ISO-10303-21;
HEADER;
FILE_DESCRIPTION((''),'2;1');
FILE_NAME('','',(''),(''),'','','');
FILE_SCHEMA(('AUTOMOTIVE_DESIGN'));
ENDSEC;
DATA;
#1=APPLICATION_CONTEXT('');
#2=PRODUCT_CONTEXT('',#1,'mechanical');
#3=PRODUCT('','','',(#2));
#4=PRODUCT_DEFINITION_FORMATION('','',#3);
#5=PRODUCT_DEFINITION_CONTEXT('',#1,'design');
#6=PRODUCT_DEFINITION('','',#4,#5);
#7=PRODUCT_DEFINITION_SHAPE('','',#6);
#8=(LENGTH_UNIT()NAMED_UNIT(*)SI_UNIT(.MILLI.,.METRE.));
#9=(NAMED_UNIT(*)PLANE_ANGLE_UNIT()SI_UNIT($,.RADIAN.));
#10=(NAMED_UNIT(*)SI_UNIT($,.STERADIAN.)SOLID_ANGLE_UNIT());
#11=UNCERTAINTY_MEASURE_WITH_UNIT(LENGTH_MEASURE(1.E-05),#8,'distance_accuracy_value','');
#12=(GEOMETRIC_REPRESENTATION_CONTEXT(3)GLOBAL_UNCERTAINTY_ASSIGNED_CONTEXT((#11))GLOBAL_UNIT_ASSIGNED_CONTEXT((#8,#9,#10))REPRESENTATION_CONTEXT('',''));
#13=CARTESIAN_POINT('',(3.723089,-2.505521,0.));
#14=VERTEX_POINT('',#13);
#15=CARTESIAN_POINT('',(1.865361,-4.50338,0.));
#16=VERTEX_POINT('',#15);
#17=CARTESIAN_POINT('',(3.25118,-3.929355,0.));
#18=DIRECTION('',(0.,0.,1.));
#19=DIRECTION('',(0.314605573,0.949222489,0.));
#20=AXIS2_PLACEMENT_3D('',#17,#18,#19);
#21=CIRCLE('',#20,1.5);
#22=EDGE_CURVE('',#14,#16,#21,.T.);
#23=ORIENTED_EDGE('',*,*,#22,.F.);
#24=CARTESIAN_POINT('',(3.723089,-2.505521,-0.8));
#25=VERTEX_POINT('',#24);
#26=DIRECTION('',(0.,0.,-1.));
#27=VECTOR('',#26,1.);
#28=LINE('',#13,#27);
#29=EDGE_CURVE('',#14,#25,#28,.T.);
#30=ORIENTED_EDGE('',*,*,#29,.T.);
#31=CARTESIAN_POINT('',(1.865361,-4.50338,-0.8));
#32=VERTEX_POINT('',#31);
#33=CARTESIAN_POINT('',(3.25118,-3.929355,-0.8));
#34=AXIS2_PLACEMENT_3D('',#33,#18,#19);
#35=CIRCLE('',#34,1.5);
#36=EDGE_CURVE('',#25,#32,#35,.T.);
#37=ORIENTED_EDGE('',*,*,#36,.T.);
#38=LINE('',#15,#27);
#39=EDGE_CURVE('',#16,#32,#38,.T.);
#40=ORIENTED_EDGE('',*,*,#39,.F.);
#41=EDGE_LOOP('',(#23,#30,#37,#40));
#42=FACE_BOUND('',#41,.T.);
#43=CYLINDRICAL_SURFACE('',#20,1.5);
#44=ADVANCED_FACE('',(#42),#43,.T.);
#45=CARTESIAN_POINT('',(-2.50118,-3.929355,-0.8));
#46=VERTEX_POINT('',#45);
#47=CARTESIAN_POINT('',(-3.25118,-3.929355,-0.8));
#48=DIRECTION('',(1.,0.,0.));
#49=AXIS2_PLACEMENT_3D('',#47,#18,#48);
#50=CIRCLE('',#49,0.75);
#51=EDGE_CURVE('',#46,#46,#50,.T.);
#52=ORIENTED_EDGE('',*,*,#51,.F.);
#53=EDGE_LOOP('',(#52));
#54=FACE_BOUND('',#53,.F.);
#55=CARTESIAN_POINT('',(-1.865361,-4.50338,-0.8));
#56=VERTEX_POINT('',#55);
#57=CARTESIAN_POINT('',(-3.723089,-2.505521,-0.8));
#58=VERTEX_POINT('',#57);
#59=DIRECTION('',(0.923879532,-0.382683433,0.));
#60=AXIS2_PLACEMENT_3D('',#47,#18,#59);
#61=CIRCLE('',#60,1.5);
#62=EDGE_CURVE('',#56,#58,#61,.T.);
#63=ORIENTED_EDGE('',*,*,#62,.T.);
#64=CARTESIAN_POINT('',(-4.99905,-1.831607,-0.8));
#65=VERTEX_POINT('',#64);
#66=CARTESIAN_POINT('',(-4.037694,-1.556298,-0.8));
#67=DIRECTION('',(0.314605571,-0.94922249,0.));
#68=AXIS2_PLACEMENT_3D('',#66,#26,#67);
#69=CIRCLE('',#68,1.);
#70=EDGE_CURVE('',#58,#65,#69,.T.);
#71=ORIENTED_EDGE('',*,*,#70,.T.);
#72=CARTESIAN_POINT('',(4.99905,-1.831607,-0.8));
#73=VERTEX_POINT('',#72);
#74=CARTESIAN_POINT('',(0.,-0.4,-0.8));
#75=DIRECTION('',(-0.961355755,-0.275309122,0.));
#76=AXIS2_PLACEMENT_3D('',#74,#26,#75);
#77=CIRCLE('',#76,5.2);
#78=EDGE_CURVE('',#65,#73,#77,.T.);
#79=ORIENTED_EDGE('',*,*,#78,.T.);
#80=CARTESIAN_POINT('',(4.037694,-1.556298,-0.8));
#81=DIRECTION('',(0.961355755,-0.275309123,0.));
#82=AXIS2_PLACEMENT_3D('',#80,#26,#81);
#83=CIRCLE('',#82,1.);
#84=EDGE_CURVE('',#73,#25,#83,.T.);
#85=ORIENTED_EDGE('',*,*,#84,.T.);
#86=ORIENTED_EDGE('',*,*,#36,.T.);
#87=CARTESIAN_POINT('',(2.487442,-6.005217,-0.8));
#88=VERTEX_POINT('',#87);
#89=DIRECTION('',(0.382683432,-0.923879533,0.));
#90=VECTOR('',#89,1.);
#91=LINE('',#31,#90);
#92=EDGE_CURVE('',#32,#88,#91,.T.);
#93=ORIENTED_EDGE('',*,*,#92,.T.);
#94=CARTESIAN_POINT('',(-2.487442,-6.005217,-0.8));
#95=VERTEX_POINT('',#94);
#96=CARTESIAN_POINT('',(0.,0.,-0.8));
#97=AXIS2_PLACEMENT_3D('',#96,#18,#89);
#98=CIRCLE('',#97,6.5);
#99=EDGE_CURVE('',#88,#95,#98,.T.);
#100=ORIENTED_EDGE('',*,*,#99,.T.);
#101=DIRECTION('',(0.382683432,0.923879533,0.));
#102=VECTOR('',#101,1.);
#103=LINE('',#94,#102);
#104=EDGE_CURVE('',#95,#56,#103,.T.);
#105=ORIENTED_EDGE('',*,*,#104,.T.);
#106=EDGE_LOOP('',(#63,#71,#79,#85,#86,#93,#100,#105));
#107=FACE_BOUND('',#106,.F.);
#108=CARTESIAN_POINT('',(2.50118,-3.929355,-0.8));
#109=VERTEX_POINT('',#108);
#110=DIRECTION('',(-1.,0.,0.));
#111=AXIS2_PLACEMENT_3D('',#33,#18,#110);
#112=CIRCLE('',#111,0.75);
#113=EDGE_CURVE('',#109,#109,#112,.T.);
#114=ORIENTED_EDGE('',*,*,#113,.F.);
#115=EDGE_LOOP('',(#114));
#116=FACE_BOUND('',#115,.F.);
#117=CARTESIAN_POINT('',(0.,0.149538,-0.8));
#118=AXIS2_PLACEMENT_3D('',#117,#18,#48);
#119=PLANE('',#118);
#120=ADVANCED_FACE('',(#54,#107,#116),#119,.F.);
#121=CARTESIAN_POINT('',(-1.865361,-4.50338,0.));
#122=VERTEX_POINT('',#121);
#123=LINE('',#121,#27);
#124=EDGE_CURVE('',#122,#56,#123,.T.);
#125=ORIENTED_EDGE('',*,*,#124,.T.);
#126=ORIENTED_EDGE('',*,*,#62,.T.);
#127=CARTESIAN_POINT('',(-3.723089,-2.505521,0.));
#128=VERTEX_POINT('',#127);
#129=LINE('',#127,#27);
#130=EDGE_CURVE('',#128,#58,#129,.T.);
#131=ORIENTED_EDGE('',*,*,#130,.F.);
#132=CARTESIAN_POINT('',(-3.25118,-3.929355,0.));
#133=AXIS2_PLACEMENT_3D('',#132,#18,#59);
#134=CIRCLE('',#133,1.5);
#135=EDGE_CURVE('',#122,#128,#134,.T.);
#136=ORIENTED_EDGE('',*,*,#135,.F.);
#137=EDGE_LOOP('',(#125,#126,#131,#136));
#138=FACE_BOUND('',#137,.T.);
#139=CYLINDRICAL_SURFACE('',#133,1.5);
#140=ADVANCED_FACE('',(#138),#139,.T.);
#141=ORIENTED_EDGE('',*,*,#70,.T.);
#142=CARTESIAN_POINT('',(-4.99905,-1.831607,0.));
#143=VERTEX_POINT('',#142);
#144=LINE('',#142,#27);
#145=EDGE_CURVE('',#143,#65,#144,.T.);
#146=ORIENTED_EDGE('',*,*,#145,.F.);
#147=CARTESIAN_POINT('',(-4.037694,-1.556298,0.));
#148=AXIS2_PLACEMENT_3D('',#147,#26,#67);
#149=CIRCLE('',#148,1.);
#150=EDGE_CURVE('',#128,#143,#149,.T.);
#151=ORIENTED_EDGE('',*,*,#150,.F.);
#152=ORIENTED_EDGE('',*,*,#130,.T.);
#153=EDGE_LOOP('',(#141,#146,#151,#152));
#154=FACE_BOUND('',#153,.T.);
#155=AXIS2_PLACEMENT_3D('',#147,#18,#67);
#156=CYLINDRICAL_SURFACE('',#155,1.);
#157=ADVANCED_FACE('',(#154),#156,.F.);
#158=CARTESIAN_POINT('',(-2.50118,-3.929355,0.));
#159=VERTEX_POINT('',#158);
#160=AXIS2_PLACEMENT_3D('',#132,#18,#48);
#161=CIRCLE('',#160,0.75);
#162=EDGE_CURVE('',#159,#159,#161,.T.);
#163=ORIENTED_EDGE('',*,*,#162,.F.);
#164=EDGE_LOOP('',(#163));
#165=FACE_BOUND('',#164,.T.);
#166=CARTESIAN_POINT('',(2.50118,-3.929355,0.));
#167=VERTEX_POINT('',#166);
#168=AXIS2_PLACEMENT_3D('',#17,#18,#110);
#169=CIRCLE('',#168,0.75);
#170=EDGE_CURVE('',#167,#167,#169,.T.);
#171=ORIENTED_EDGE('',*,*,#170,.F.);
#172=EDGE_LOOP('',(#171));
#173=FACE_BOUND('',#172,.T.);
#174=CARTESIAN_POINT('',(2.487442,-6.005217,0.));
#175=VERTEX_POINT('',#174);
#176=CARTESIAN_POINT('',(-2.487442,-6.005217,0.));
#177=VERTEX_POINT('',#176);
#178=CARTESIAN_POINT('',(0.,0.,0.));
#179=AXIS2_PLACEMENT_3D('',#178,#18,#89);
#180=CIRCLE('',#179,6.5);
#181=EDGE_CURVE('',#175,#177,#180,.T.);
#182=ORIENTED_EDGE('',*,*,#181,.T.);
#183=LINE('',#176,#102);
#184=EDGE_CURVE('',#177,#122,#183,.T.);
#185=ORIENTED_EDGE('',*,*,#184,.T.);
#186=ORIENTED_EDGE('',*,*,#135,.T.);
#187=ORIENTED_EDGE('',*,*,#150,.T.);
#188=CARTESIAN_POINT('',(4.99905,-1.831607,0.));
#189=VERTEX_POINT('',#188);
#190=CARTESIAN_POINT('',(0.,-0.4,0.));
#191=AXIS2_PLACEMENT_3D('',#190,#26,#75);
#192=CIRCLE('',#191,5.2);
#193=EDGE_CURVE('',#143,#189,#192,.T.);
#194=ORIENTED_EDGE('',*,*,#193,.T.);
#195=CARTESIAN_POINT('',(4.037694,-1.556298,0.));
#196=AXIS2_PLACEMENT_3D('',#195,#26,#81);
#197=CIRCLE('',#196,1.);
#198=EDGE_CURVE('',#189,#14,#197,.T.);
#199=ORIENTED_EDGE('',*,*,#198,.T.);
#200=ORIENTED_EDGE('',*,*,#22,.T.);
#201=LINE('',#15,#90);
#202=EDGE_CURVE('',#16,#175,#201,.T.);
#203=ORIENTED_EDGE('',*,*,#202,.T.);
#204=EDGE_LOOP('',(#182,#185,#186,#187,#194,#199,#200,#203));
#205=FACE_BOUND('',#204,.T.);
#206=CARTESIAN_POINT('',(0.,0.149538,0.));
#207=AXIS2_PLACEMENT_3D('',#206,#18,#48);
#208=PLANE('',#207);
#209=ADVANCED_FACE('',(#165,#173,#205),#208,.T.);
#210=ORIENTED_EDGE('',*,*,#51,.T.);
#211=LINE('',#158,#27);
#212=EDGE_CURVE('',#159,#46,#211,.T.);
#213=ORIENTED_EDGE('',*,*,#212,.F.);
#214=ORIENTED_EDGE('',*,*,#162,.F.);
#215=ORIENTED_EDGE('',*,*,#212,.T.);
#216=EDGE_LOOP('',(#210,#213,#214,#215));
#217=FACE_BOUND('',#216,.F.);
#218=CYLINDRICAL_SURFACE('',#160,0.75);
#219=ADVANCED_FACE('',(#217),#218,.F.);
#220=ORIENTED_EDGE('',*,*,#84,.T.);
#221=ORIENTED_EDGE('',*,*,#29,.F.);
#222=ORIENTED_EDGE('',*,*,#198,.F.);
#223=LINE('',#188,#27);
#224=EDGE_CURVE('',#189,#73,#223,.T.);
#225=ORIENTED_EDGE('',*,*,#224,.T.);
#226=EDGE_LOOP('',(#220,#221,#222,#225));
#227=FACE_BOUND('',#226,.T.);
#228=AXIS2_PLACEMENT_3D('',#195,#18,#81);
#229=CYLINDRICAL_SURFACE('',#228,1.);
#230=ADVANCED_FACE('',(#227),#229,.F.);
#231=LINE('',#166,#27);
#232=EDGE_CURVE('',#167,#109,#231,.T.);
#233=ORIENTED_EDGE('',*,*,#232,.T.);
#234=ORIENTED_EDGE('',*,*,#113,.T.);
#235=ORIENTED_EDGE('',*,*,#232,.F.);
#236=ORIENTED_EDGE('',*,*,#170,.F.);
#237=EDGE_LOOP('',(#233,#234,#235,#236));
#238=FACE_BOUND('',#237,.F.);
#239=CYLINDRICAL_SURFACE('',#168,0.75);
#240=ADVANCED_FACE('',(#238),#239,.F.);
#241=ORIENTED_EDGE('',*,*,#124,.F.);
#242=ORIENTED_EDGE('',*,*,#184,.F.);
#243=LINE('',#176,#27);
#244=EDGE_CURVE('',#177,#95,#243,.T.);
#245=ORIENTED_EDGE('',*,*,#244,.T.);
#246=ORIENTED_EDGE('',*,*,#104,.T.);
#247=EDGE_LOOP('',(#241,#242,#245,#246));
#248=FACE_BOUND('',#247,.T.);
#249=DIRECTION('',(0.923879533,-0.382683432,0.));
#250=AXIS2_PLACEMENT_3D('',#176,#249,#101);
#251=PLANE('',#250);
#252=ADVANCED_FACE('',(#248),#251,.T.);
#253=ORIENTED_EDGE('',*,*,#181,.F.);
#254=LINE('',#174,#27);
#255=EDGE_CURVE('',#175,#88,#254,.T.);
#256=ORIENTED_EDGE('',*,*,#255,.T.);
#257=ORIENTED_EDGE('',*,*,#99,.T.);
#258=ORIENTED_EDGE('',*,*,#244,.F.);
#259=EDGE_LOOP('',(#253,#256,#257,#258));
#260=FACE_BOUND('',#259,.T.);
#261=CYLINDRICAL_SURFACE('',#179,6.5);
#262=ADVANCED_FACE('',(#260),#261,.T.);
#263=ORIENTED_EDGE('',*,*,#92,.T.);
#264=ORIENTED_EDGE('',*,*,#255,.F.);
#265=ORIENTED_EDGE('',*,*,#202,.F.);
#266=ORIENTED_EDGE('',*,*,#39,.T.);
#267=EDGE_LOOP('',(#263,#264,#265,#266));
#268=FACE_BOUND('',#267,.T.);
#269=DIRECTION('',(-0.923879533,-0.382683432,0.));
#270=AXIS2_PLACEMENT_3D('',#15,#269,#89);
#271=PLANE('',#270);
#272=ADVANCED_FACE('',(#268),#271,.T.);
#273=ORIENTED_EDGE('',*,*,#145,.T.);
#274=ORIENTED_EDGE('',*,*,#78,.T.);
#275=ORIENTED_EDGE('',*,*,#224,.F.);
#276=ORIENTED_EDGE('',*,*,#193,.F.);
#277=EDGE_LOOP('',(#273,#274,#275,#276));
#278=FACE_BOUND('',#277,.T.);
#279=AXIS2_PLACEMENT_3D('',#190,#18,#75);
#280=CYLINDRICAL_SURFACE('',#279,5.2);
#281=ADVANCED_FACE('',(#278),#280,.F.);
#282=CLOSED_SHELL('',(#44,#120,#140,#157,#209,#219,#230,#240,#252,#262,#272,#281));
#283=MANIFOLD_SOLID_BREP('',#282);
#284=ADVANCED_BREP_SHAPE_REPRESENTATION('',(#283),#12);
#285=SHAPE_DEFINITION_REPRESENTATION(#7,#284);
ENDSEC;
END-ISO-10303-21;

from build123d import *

# Parameters (mm, degrees)
SKETCH1_R  = 0.75
BODY_DEPTH = 0.8


with BuildPart() as part:
    # Sketch1 → Body (new body)
    with BuildSketch(Plane.XY):
        with BuildLine():
            Line((1.865360941, -4.503379682), (2.48744231, -6.005216961))
            ThreePointArc((2.48744231, -6.005216961), (0, 6.5), (-2.48744231, -6.005216961))
            Line((-2.48744231, -6.005216961), (-1.865360941, -4.503379682))
            ThreePointArc((-1.865360941, -4.503379682), (-2.152695679, -2.907918451), (-3.723088598, -2.5055208))
            ThreePointArc((-3.723088598, -2.5055208), (-4.504717999, -2.440543041), (-4.999049926, -1.831607432))
            ThreePointArc((-4.999049926, -1.831607432), (0, 4.8), (4.999049926, -1.831607432))
            ThreePointArc((4.999049926, -1.831607432), (4.504717999, -2.440543041), (3.723088598, -2.5055208))
            ThreePointArc((3.723088598, -2.5055208), (2.152695679, -2.907918451), (1.865360941, -4.503379682))
        make_face()
        with Locations(Location((3.25118024, -3.929354533, 0), (0, 0, 180))):
            Circle(SKETCH1_R, mode=Mode.SUBTRACT)
        with Locations((-3.25118024, -3.929354533)):
            Circle(SKETCH1_R, mode=Mode.SUBTRACT)
    extrude(amount=-BODY_DEPTH)


solid = part.part
